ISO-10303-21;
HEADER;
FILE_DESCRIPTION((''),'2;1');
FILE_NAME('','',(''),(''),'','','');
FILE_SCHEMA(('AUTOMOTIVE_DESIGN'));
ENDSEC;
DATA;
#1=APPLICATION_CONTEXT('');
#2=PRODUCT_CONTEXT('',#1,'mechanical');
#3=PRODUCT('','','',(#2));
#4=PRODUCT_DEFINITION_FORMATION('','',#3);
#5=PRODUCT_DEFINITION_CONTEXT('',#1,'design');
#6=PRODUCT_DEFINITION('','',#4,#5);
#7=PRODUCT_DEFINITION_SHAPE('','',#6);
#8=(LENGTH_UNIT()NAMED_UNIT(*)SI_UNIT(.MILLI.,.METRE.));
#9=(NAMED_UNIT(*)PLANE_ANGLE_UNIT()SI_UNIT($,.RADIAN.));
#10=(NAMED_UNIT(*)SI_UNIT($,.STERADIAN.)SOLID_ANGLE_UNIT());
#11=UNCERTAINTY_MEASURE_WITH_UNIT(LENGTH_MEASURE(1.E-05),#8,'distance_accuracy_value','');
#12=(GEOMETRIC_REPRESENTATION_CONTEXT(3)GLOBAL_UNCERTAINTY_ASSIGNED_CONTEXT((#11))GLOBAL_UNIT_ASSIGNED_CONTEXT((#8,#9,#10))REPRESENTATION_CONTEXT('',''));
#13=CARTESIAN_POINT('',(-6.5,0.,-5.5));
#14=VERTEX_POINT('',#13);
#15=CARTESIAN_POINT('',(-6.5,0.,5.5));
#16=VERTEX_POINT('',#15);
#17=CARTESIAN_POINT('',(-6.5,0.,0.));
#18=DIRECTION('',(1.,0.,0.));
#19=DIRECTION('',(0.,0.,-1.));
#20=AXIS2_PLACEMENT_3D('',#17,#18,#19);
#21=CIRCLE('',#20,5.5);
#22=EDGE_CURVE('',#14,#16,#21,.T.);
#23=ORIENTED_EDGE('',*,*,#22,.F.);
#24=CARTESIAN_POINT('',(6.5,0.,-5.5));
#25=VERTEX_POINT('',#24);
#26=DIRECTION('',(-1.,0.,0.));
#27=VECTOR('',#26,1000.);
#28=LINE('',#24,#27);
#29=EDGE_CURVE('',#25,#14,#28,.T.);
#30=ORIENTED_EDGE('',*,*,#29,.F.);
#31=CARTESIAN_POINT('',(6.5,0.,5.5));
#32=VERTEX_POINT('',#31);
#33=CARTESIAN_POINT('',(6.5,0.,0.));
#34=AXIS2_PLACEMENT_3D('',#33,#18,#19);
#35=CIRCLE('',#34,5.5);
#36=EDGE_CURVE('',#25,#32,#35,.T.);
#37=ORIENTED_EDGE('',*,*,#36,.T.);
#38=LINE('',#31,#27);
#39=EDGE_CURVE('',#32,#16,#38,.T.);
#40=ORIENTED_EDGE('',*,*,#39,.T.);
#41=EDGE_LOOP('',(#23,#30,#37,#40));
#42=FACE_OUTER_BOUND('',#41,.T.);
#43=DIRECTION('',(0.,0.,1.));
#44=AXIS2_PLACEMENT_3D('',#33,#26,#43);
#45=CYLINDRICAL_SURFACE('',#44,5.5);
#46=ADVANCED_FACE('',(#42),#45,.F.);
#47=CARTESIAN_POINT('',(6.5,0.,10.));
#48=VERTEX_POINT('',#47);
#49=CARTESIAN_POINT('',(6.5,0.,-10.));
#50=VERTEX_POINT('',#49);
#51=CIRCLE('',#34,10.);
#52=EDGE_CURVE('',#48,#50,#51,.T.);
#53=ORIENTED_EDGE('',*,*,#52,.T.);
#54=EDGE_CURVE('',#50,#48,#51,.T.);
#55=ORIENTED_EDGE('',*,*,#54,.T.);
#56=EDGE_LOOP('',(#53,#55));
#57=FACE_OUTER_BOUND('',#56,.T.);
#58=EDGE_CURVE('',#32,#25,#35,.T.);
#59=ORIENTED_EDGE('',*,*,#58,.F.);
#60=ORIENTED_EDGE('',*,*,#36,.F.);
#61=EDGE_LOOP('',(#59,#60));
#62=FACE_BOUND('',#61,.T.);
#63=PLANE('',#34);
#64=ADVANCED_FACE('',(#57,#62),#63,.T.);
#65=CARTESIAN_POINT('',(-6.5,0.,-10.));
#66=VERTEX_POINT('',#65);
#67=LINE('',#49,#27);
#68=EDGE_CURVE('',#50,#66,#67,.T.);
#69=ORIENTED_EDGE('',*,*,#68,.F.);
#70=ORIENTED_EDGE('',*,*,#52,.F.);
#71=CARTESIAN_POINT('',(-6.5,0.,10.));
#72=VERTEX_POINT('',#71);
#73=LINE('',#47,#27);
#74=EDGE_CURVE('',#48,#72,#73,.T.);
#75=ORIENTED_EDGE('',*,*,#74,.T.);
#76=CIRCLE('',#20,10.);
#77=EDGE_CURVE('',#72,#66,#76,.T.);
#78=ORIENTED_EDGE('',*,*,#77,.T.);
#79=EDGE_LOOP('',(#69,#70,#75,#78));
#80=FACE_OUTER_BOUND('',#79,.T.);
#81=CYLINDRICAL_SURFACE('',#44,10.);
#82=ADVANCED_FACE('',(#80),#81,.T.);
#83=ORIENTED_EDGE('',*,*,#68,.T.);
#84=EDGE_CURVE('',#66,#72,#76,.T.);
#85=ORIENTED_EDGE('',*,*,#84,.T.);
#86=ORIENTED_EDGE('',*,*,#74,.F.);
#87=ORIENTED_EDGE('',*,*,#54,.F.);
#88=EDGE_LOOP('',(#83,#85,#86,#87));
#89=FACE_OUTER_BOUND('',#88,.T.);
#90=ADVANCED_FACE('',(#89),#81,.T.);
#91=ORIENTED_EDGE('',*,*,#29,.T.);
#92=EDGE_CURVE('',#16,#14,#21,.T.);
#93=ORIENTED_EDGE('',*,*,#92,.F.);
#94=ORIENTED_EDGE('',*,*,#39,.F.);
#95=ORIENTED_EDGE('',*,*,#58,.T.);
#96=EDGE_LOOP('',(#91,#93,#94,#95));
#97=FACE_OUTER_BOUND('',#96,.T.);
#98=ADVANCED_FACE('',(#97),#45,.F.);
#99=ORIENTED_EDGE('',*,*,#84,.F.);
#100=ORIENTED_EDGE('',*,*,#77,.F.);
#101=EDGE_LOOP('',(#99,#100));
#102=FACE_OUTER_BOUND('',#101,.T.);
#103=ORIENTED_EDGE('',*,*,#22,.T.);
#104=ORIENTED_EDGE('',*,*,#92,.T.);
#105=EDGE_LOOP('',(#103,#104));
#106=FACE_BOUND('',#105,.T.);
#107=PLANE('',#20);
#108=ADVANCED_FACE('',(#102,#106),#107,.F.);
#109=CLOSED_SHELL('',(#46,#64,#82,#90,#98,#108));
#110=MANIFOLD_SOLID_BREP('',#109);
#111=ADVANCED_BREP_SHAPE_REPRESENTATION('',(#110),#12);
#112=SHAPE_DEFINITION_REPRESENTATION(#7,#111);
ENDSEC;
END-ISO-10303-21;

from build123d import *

# Parameters (mm, degrees)
SKETCH2_R           = 10
SKETCH2_R_2         = 5.5
BOSS_EXTRUDE2_DEPTH = 6.5


with BuildPart() as part:
    # Sketch2 → Boss-Extrude2 (new, symmetric)
    with BuildSketch(Plane(origin=(0, 0, 0), x_dir=(0, 0, -1), z_dir=(1, 0, 0))):
        with Locations(Location((0, 0, 0), (0, 0, 180))):
            Circle(SKETCH2_R)
        with Locations(Location((0, 0, 0), (0, 0, 180))):
            Circle(SKETCH2_R_2, mode=Mode.SUBTRACT)
    extrude(amount=BOSS_EXTRUDE2_DEPTH, both=True)


solid = part.part
